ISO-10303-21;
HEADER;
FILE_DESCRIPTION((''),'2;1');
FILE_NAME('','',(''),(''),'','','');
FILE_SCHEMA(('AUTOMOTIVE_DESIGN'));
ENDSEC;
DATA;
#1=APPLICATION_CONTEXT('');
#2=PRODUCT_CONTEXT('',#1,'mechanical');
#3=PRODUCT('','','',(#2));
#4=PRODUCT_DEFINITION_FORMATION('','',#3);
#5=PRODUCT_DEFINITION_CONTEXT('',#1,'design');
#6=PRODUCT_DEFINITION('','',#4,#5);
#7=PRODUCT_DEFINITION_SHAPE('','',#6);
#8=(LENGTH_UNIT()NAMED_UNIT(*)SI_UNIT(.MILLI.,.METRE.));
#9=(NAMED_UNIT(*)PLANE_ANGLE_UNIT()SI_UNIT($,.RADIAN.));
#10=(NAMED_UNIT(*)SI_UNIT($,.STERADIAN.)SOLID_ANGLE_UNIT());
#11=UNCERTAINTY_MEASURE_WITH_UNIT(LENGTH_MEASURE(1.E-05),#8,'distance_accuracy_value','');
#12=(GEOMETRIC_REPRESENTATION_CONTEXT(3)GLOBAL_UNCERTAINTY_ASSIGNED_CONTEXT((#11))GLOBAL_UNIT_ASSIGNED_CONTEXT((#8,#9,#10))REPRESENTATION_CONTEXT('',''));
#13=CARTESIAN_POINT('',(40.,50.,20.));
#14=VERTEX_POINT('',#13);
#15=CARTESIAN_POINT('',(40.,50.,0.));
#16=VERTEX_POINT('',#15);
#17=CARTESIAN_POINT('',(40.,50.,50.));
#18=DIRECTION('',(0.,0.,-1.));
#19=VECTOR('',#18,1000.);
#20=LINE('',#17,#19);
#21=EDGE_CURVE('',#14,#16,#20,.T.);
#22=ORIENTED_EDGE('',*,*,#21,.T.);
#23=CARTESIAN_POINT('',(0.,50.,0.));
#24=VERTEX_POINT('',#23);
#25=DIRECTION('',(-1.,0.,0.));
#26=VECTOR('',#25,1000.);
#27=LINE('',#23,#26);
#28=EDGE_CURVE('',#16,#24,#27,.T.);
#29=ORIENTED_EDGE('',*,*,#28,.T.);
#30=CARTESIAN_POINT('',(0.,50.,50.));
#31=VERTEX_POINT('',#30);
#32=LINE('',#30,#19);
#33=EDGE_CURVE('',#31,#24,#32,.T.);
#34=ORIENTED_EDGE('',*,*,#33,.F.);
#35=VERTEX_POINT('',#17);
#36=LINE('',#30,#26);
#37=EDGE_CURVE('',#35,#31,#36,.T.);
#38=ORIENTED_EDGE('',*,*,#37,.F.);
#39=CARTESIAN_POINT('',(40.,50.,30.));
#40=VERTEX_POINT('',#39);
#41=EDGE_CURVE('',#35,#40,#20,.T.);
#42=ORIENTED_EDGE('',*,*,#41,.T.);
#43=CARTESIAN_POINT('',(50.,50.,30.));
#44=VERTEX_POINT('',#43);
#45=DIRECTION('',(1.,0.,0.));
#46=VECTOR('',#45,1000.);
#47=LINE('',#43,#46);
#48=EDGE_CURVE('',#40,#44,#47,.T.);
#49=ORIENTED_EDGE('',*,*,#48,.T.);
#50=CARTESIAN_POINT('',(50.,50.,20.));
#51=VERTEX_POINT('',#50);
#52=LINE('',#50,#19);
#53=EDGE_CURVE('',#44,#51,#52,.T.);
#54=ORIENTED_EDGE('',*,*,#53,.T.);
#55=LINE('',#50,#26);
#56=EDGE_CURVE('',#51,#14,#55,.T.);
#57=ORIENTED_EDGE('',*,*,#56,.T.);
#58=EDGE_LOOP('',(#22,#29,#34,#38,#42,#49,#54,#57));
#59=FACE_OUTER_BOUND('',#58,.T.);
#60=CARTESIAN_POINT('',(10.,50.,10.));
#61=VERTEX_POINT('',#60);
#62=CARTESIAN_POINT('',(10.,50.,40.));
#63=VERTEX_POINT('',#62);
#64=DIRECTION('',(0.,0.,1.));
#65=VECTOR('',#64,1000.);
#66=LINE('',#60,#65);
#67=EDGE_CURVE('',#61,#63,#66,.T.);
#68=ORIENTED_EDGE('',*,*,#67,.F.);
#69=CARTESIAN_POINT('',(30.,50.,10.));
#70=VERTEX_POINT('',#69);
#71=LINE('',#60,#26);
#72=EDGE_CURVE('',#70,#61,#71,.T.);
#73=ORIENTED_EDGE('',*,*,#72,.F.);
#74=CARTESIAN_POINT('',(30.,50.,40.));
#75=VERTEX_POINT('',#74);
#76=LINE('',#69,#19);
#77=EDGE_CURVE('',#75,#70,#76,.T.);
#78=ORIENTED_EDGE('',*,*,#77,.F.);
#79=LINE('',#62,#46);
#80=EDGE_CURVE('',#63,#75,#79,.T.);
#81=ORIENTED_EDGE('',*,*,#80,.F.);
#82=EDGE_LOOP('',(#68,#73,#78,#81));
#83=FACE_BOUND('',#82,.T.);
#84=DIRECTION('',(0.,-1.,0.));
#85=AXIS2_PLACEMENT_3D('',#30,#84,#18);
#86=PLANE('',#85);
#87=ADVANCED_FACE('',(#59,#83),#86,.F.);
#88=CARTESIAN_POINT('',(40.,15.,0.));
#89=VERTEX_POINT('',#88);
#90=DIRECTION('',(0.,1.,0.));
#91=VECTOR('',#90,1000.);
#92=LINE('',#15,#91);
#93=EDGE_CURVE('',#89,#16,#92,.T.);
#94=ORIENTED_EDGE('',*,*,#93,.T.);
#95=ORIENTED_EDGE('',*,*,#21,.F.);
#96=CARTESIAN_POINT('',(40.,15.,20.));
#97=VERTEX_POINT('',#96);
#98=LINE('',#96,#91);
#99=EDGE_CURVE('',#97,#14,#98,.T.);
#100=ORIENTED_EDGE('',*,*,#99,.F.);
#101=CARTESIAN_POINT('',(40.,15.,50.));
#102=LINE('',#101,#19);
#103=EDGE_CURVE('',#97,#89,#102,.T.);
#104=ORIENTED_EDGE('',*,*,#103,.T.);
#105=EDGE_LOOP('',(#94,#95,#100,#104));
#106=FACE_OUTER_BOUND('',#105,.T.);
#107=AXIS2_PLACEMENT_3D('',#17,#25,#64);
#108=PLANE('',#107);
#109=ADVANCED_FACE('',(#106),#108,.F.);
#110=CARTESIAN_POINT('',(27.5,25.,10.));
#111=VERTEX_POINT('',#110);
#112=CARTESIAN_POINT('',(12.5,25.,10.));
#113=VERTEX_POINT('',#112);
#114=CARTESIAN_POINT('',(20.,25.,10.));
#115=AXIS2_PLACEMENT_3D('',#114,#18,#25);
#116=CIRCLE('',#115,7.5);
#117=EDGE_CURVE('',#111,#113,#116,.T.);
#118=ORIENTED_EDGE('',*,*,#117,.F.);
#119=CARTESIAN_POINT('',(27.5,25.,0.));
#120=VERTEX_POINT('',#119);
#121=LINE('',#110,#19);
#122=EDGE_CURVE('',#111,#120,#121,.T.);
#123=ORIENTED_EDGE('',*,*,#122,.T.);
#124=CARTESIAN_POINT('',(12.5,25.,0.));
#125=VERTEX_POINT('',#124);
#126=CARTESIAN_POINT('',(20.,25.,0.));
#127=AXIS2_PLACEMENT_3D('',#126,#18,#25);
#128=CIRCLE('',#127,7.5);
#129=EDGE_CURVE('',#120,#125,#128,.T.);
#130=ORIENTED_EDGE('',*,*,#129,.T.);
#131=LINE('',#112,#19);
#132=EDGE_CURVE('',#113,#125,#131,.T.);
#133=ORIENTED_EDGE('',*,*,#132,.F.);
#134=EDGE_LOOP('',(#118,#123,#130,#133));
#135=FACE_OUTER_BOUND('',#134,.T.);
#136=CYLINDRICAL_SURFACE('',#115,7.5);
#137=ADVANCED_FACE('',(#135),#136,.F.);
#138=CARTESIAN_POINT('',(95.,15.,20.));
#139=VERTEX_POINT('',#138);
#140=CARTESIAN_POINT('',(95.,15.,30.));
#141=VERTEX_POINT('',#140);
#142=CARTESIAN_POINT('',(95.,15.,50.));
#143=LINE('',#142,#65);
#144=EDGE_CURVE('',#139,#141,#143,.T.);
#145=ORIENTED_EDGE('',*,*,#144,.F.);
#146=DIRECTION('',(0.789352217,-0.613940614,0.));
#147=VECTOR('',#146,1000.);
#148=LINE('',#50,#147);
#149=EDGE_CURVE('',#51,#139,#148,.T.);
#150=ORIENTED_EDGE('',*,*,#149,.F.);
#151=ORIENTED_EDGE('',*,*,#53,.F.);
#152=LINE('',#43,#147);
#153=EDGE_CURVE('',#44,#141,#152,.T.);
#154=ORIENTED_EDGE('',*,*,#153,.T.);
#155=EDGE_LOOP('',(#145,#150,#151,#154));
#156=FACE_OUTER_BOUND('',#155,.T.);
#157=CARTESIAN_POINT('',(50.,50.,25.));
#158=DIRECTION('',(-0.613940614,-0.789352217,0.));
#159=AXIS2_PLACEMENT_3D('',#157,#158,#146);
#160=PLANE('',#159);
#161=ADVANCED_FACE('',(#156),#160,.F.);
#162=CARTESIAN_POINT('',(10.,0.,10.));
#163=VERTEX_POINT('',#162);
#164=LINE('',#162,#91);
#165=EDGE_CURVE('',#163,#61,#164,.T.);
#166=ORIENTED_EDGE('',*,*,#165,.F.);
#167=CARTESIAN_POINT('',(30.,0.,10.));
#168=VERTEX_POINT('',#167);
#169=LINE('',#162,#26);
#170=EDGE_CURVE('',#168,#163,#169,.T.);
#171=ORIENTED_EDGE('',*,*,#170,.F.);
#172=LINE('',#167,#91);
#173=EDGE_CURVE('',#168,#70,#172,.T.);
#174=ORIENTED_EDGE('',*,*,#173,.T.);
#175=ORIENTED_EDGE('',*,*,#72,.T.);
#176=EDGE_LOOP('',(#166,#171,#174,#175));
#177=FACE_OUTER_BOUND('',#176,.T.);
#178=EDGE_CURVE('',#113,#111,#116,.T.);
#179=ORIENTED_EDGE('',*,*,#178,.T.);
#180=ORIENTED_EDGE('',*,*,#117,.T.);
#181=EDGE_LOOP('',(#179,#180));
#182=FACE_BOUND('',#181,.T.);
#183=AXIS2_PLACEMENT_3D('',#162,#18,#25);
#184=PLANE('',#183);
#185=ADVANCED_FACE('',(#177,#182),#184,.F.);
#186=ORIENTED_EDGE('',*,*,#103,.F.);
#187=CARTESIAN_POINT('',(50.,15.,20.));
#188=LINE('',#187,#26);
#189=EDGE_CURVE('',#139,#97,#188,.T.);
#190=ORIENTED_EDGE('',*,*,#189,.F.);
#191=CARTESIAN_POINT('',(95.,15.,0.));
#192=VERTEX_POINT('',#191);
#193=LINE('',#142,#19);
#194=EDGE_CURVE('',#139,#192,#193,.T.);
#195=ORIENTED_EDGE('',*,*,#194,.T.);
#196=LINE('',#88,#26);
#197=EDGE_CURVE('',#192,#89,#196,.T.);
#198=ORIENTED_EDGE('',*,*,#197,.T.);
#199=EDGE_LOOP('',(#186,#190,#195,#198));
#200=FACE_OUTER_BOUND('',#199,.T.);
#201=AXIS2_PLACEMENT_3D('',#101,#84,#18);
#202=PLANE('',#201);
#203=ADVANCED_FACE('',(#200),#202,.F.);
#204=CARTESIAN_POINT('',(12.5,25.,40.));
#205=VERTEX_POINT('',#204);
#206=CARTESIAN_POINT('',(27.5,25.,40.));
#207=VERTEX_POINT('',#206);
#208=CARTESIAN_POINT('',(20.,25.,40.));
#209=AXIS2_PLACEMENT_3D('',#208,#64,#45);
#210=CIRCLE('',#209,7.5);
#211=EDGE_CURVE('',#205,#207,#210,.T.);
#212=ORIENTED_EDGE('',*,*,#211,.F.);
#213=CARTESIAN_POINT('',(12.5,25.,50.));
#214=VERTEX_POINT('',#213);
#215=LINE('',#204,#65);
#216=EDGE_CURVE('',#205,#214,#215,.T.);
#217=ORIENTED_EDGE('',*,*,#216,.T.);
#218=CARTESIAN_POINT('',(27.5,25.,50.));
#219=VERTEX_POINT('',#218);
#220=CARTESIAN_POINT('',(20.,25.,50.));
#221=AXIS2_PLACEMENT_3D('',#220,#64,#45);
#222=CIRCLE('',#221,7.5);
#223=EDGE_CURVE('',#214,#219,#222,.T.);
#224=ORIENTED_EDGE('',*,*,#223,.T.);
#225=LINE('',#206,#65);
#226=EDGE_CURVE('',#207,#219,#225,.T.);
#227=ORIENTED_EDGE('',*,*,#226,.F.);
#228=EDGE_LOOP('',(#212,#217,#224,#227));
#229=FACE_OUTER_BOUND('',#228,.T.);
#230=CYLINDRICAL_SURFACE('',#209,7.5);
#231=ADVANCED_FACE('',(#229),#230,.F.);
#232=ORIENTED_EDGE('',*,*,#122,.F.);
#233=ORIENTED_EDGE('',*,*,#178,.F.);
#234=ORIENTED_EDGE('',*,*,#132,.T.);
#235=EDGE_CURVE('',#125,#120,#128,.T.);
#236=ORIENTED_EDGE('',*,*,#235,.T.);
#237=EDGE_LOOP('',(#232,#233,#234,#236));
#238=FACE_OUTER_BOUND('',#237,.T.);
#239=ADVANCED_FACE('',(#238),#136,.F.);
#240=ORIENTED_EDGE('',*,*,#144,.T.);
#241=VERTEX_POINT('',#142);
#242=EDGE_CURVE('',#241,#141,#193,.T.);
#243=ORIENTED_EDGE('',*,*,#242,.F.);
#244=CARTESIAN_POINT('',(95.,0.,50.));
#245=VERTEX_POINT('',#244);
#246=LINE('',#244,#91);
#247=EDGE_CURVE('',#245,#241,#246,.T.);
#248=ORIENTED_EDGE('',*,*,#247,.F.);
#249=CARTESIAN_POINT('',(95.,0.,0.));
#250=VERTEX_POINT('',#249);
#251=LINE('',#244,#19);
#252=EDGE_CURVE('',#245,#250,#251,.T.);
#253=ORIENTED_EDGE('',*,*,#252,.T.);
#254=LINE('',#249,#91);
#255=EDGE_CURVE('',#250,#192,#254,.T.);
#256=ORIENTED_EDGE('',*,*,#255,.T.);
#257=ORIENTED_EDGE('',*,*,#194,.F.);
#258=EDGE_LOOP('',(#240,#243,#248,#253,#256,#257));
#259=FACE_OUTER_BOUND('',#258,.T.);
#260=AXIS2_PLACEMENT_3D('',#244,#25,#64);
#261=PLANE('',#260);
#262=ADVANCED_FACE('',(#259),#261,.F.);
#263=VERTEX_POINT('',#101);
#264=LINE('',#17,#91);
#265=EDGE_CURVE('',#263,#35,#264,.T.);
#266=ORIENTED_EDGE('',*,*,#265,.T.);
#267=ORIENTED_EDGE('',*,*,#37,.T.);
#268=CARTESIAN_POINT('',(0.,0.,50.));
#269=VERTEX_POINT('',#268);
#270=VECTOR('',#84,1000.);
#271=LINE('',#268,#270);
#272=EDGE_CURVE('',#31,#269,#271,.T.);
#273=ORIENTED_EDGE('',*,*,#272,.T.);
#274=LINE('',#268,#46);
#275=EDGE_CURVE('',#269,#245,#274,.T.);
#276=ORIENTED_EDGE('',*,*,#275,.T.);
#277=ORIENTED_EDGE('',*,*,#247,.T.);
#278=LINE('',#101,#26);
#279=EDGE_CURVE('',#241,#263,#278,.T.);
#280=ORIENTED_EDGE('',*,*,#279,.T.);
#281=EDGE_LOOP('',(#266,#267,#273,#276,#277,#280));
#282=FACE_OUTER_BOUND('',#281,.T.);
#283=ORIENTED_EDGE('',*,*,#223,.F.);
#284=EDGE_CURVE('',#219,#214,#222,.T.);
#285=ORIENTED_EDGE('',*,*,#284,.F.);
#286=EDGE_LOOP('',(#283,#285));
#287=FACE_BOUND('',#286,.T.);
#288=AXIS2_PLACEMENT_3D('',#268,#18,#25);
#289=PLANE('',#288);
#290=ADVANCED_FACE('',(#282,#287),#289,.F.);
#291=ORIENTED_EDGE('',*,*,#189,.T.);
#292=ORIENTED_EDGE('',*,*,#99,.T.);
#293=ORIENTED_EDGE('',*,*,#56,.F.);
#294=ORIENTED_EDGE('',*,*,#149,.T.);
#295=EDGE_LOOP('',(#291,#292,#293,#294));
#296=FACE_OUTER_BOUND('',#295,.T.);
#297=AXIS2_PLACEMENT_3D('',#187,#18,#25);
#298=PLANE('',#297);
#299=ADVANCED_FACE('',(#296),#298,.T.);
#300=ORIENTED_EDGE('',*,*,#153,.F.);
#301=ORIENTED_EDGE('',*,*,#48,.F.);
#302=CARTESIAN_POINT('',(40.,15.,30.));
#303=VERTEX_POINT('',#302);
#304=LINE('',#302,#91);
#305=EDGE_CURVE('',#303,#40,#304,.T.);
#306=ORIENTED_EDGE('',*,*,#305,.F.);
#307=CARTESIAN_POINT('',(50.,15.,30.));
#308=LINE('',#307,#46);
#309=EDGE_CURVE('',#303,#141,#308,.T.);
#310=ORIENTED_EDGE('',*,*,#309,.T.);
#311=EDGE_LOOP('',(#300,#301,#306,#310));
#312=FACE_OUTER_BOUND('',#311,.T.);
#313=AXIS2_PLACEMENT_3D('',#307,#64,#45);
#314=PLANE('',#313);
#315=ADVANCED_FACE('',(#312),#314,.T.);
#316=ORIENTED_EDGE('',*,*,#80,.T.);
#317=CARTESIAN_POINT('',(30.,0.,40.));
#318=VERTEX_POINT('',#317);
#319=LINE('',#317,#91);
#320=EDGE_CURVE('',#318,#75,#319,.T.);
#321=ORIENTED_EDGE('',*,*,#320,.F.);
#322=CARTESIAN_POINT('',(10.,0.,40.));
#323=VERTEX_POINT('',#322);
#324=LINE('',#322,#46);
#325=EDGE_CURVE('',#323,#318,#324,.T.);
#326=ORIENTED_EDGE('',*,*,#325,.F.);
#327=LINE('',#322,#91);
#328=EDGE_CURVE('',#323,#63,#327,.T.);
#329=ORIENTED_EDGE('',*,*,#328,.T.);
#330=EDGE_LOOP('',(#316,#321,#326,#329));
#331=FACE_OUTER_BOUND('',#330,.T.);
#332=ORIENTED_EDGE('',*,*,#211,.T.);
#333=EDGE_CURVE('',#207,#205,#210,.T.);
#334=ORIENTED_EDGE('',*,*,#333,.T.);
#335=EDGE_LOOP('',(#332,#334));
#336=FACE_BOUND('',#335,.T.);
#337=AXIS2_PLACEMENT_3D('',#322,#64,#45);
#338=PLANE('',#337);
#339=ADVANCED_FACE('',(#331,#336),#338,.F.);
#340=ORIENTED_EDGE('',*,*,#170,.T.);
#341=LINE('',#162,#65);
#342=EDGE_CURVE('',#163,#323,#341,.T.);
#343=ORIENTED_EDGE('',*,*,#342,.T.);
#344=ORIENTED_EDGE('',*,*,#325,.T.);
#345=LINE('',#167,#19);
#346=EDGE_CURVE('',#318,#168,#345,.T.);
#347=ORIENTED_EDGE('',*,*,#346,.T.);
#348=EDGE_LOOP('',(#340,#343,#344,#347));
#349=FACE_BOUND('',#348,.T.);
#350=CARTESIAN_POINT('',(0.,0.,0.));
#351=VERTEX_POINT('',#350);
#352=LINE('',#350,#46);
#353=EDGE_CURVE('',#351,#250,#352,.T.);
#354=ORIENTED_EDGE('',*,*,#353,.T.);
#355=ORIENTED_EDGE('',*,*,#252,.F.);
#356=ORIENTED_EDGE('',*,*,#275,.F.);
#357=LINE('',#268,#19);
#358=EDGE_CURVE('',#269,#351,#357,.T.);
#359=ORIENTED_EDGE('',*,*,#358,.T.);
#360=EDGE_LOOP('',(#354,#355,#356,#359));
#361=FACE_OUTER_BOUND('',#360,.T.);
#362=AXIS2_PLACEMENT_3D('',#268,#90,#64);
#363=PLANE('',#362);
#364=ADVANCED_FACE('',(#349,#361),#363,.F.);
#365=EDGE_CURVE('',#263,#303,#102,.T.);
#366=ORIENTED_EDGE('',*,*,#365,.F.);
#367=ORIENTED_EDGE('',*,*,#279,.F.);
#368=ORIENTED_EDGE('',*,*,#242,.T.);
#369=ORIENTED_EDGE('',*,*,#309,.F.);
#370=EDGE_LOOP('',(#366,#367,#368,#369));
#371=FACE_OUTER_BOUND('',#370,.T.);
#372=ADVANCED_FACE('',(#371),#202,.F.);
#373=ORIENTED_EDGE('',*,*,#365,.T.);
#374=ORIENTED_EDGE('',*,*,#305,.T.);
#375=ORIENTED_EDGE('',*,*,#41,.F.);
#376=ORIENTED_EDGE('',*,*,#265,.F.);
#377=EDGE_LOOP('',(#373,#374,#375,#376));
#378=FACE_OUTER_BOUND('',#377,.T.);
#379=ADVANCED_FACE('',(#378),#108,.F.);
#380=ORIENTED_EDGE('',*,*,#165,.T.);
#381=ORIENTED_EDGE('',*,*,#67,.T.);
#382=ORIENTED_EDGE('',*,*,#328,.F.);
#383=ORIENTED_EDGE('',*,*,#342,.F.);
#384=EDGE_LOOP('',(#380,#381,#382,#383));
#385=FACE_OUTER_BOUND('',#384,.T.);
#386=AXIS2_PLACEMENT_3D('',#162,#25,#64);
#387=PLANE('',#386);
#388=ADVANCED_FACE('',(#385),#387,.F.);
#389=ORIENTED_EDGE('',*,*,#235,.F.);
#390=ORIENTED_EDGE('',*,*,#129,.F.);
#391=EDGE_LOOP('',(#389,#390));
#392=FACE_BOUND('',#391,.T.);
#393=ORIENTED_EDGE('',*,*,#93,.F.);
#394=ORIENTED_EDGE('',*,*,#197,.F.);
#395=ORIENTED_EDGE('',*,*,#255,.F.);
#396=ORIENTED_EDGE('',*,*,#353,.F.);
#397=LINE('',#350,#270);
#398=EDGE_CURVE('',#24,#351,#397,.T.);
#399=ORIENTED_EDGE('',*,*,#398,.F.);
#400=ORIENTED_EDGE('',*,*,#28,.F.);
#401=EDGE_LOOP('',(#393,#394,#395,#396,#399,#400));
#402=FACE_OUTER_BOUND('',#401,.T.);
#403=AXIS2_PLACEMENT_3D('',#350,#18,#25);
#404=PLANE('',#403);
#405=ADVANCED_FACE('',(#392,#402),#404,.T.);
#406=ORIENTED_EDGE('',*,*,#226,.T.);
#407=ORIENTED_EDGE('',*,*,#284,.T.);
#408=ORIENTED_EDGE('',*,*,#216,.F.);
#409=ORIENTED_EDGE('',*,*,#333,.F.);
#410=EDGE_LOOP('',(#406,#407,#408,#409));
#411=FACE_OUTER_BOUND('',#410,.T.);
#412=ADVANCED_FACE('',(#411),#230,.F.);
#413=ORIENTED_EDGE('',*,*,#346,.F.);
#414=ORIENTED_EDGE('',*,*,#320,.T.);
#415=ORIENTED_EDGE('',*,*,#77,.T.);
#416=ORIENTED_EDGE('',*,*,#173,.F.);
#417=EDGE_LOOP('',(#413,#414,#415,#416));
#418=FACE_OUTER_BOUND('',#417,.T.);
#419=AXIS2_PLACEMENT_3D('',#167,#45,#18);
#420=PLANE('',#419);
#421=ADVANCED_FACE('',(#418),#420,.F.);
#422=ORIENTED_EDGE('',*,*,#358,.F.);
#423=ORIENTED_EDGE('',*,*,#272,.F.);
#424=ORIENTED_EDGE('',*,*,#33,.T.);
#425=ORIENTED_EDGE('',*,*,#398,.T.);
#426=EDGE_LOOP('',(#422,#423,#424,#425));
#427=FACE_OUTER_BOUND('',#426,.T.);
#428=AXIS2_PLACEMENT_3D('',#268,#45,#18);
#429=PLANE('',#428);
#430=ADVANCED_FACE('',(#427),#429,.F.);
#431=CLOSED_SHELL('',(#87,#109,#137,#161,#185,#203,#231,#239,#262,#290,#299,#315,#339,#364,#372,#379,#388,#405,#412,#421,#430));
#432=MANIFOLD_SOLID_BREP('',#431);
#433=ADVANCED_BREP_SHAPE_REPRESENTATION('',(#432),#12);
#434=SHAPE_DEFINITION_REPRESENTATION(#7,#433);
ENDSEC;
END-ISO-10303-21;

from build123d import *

# Parameters (mm, degrees)
BRACKET_BASE_50MM_DEPTH    = 50
HOLE_1_SKETCH_R            = 7.5
HOLE_1_CUT_10MM_DEEP_DEPTH = 10
HOLE_START                 = -10
HOLE_2_SKETCH_R            = 7.5
HOLE_2_CUT_10MM_DEEP_DEPTH = 10
RAISED_BOSS_SKETCH_W       = 10
RAISED_BOSS_SKETCH_H       = 10
RAISED_BOSS_35MM_DEPTH     = 35
GUSSET_RIB_10MM_REACH      = 112.227
GUSSET_RIB_SKETCH_WALL_W   = 279.462848106
GUSSET_RIB_SKETCH_WALL_H   = 10
SQUARE_POCKET_SKETCH_W     = 20
SQUARE_POCKET_SKETCH_H     = 30
SQUARE_POCKET_CUT_DEPTH    = 119.427192823


with BuildPart() as part:
    # Bracket Profile Sketch → Bracket Base 50mm (new body)
    with BuildSketch(Plane.XY):
        Polygon((0, 0), (95, 0), (95, 15), (40, 15), (40, 50), (0, 50), align=None)
    extrude(amount=BRACKET_BASE_50MM_DEPTH)

    # Hole 1 Sketch → Hole 1 Cut 10mm Deep (cut)
    with BuildSketch(Plane.XY.offset(50)):
        with Locations((20, 25)):
            Circle(HOLE_1_SKETCH_R)
    extrude(amount=-HOLE_1_CUT_10MM_DEEP_DEPTH, mode=Mode.SUBTRACT)

    # Hole 2 Sketch → Hole 2 Cut 10mm Deep (cut)
    with BuildSketch(Plane(origin=(0, 0, 0), x_dir=(-1, 0, 0), z_dir=(0, 0, -1)).offset(HOLE_START)):
        with Locations(Location((-20, 25, 0), (0, 0, 180))):
            Circle(HOLE_2_SKETCH_R)
    extrude(amount=HOLE_2_CUT_10MM_DEEP_DEPTH, mode=Mode.SUBTRACT)

    # Raised Boss Sketch → Raised Boss 35mm (add)
    with BuildSketch(Plane(origin=(0, 50, 0), x_dir=(1, 0, 0), z_dir=(0, 1, 0))):
        with Locations((45, -25)):
            Rectangle(RAISED_BOSS_SKETCH_W, RAISED_BOSS_SKETCH_H)
    extrude(amount=-RAISED_BOSS_35MM_DEPTH)

    # Gusset Rib Sketch wall → Gusset Rib 10mm (add, up to next)
    with BuildSketch(Plane(origin=(72.5, 32.5, 25), x_dir=(0.789352217376, -0.613940613515, 0), z_dir=(0.613940613515, 0.789352217376, 0)), mode=Mode.PRIVATE) as gusset_rib_10mm_sk1:
        Rectangle(GUSSET_RIB_SKETCH_WALL_W, GUSSET_RIB_SKETCH_WALL_H)
    gusset_rib_10mm_tool1 = extrude(gusset_rib_10mm_sk1.sketch, amount=-GUSSET_RIB_10MM_REACH, mode=Mode.PRIVATE) - part.part
    add(gusset_rib_10mm_tool1.solids().sort_by_distance((72.5, 32.5, 25))[0])

    # Square Pocket Sketch → Square Pocket Cut (cut, through all)
    with BuildSketch(Plane(origin=(0, 50, 0), x_dir=(1, 0, 0), z_dir=(0, 1, 0))):
        with Locations((20, -25)):
            Rectangle(SQUARE_POCKET_SKETCH_W, SQUARE_POCKET_SKETCH_H)
    extrude(amount=-SQUARE_POCKET_CUT_DEPTH, mode=Mode.SUBTRACT)


solid = part.part
